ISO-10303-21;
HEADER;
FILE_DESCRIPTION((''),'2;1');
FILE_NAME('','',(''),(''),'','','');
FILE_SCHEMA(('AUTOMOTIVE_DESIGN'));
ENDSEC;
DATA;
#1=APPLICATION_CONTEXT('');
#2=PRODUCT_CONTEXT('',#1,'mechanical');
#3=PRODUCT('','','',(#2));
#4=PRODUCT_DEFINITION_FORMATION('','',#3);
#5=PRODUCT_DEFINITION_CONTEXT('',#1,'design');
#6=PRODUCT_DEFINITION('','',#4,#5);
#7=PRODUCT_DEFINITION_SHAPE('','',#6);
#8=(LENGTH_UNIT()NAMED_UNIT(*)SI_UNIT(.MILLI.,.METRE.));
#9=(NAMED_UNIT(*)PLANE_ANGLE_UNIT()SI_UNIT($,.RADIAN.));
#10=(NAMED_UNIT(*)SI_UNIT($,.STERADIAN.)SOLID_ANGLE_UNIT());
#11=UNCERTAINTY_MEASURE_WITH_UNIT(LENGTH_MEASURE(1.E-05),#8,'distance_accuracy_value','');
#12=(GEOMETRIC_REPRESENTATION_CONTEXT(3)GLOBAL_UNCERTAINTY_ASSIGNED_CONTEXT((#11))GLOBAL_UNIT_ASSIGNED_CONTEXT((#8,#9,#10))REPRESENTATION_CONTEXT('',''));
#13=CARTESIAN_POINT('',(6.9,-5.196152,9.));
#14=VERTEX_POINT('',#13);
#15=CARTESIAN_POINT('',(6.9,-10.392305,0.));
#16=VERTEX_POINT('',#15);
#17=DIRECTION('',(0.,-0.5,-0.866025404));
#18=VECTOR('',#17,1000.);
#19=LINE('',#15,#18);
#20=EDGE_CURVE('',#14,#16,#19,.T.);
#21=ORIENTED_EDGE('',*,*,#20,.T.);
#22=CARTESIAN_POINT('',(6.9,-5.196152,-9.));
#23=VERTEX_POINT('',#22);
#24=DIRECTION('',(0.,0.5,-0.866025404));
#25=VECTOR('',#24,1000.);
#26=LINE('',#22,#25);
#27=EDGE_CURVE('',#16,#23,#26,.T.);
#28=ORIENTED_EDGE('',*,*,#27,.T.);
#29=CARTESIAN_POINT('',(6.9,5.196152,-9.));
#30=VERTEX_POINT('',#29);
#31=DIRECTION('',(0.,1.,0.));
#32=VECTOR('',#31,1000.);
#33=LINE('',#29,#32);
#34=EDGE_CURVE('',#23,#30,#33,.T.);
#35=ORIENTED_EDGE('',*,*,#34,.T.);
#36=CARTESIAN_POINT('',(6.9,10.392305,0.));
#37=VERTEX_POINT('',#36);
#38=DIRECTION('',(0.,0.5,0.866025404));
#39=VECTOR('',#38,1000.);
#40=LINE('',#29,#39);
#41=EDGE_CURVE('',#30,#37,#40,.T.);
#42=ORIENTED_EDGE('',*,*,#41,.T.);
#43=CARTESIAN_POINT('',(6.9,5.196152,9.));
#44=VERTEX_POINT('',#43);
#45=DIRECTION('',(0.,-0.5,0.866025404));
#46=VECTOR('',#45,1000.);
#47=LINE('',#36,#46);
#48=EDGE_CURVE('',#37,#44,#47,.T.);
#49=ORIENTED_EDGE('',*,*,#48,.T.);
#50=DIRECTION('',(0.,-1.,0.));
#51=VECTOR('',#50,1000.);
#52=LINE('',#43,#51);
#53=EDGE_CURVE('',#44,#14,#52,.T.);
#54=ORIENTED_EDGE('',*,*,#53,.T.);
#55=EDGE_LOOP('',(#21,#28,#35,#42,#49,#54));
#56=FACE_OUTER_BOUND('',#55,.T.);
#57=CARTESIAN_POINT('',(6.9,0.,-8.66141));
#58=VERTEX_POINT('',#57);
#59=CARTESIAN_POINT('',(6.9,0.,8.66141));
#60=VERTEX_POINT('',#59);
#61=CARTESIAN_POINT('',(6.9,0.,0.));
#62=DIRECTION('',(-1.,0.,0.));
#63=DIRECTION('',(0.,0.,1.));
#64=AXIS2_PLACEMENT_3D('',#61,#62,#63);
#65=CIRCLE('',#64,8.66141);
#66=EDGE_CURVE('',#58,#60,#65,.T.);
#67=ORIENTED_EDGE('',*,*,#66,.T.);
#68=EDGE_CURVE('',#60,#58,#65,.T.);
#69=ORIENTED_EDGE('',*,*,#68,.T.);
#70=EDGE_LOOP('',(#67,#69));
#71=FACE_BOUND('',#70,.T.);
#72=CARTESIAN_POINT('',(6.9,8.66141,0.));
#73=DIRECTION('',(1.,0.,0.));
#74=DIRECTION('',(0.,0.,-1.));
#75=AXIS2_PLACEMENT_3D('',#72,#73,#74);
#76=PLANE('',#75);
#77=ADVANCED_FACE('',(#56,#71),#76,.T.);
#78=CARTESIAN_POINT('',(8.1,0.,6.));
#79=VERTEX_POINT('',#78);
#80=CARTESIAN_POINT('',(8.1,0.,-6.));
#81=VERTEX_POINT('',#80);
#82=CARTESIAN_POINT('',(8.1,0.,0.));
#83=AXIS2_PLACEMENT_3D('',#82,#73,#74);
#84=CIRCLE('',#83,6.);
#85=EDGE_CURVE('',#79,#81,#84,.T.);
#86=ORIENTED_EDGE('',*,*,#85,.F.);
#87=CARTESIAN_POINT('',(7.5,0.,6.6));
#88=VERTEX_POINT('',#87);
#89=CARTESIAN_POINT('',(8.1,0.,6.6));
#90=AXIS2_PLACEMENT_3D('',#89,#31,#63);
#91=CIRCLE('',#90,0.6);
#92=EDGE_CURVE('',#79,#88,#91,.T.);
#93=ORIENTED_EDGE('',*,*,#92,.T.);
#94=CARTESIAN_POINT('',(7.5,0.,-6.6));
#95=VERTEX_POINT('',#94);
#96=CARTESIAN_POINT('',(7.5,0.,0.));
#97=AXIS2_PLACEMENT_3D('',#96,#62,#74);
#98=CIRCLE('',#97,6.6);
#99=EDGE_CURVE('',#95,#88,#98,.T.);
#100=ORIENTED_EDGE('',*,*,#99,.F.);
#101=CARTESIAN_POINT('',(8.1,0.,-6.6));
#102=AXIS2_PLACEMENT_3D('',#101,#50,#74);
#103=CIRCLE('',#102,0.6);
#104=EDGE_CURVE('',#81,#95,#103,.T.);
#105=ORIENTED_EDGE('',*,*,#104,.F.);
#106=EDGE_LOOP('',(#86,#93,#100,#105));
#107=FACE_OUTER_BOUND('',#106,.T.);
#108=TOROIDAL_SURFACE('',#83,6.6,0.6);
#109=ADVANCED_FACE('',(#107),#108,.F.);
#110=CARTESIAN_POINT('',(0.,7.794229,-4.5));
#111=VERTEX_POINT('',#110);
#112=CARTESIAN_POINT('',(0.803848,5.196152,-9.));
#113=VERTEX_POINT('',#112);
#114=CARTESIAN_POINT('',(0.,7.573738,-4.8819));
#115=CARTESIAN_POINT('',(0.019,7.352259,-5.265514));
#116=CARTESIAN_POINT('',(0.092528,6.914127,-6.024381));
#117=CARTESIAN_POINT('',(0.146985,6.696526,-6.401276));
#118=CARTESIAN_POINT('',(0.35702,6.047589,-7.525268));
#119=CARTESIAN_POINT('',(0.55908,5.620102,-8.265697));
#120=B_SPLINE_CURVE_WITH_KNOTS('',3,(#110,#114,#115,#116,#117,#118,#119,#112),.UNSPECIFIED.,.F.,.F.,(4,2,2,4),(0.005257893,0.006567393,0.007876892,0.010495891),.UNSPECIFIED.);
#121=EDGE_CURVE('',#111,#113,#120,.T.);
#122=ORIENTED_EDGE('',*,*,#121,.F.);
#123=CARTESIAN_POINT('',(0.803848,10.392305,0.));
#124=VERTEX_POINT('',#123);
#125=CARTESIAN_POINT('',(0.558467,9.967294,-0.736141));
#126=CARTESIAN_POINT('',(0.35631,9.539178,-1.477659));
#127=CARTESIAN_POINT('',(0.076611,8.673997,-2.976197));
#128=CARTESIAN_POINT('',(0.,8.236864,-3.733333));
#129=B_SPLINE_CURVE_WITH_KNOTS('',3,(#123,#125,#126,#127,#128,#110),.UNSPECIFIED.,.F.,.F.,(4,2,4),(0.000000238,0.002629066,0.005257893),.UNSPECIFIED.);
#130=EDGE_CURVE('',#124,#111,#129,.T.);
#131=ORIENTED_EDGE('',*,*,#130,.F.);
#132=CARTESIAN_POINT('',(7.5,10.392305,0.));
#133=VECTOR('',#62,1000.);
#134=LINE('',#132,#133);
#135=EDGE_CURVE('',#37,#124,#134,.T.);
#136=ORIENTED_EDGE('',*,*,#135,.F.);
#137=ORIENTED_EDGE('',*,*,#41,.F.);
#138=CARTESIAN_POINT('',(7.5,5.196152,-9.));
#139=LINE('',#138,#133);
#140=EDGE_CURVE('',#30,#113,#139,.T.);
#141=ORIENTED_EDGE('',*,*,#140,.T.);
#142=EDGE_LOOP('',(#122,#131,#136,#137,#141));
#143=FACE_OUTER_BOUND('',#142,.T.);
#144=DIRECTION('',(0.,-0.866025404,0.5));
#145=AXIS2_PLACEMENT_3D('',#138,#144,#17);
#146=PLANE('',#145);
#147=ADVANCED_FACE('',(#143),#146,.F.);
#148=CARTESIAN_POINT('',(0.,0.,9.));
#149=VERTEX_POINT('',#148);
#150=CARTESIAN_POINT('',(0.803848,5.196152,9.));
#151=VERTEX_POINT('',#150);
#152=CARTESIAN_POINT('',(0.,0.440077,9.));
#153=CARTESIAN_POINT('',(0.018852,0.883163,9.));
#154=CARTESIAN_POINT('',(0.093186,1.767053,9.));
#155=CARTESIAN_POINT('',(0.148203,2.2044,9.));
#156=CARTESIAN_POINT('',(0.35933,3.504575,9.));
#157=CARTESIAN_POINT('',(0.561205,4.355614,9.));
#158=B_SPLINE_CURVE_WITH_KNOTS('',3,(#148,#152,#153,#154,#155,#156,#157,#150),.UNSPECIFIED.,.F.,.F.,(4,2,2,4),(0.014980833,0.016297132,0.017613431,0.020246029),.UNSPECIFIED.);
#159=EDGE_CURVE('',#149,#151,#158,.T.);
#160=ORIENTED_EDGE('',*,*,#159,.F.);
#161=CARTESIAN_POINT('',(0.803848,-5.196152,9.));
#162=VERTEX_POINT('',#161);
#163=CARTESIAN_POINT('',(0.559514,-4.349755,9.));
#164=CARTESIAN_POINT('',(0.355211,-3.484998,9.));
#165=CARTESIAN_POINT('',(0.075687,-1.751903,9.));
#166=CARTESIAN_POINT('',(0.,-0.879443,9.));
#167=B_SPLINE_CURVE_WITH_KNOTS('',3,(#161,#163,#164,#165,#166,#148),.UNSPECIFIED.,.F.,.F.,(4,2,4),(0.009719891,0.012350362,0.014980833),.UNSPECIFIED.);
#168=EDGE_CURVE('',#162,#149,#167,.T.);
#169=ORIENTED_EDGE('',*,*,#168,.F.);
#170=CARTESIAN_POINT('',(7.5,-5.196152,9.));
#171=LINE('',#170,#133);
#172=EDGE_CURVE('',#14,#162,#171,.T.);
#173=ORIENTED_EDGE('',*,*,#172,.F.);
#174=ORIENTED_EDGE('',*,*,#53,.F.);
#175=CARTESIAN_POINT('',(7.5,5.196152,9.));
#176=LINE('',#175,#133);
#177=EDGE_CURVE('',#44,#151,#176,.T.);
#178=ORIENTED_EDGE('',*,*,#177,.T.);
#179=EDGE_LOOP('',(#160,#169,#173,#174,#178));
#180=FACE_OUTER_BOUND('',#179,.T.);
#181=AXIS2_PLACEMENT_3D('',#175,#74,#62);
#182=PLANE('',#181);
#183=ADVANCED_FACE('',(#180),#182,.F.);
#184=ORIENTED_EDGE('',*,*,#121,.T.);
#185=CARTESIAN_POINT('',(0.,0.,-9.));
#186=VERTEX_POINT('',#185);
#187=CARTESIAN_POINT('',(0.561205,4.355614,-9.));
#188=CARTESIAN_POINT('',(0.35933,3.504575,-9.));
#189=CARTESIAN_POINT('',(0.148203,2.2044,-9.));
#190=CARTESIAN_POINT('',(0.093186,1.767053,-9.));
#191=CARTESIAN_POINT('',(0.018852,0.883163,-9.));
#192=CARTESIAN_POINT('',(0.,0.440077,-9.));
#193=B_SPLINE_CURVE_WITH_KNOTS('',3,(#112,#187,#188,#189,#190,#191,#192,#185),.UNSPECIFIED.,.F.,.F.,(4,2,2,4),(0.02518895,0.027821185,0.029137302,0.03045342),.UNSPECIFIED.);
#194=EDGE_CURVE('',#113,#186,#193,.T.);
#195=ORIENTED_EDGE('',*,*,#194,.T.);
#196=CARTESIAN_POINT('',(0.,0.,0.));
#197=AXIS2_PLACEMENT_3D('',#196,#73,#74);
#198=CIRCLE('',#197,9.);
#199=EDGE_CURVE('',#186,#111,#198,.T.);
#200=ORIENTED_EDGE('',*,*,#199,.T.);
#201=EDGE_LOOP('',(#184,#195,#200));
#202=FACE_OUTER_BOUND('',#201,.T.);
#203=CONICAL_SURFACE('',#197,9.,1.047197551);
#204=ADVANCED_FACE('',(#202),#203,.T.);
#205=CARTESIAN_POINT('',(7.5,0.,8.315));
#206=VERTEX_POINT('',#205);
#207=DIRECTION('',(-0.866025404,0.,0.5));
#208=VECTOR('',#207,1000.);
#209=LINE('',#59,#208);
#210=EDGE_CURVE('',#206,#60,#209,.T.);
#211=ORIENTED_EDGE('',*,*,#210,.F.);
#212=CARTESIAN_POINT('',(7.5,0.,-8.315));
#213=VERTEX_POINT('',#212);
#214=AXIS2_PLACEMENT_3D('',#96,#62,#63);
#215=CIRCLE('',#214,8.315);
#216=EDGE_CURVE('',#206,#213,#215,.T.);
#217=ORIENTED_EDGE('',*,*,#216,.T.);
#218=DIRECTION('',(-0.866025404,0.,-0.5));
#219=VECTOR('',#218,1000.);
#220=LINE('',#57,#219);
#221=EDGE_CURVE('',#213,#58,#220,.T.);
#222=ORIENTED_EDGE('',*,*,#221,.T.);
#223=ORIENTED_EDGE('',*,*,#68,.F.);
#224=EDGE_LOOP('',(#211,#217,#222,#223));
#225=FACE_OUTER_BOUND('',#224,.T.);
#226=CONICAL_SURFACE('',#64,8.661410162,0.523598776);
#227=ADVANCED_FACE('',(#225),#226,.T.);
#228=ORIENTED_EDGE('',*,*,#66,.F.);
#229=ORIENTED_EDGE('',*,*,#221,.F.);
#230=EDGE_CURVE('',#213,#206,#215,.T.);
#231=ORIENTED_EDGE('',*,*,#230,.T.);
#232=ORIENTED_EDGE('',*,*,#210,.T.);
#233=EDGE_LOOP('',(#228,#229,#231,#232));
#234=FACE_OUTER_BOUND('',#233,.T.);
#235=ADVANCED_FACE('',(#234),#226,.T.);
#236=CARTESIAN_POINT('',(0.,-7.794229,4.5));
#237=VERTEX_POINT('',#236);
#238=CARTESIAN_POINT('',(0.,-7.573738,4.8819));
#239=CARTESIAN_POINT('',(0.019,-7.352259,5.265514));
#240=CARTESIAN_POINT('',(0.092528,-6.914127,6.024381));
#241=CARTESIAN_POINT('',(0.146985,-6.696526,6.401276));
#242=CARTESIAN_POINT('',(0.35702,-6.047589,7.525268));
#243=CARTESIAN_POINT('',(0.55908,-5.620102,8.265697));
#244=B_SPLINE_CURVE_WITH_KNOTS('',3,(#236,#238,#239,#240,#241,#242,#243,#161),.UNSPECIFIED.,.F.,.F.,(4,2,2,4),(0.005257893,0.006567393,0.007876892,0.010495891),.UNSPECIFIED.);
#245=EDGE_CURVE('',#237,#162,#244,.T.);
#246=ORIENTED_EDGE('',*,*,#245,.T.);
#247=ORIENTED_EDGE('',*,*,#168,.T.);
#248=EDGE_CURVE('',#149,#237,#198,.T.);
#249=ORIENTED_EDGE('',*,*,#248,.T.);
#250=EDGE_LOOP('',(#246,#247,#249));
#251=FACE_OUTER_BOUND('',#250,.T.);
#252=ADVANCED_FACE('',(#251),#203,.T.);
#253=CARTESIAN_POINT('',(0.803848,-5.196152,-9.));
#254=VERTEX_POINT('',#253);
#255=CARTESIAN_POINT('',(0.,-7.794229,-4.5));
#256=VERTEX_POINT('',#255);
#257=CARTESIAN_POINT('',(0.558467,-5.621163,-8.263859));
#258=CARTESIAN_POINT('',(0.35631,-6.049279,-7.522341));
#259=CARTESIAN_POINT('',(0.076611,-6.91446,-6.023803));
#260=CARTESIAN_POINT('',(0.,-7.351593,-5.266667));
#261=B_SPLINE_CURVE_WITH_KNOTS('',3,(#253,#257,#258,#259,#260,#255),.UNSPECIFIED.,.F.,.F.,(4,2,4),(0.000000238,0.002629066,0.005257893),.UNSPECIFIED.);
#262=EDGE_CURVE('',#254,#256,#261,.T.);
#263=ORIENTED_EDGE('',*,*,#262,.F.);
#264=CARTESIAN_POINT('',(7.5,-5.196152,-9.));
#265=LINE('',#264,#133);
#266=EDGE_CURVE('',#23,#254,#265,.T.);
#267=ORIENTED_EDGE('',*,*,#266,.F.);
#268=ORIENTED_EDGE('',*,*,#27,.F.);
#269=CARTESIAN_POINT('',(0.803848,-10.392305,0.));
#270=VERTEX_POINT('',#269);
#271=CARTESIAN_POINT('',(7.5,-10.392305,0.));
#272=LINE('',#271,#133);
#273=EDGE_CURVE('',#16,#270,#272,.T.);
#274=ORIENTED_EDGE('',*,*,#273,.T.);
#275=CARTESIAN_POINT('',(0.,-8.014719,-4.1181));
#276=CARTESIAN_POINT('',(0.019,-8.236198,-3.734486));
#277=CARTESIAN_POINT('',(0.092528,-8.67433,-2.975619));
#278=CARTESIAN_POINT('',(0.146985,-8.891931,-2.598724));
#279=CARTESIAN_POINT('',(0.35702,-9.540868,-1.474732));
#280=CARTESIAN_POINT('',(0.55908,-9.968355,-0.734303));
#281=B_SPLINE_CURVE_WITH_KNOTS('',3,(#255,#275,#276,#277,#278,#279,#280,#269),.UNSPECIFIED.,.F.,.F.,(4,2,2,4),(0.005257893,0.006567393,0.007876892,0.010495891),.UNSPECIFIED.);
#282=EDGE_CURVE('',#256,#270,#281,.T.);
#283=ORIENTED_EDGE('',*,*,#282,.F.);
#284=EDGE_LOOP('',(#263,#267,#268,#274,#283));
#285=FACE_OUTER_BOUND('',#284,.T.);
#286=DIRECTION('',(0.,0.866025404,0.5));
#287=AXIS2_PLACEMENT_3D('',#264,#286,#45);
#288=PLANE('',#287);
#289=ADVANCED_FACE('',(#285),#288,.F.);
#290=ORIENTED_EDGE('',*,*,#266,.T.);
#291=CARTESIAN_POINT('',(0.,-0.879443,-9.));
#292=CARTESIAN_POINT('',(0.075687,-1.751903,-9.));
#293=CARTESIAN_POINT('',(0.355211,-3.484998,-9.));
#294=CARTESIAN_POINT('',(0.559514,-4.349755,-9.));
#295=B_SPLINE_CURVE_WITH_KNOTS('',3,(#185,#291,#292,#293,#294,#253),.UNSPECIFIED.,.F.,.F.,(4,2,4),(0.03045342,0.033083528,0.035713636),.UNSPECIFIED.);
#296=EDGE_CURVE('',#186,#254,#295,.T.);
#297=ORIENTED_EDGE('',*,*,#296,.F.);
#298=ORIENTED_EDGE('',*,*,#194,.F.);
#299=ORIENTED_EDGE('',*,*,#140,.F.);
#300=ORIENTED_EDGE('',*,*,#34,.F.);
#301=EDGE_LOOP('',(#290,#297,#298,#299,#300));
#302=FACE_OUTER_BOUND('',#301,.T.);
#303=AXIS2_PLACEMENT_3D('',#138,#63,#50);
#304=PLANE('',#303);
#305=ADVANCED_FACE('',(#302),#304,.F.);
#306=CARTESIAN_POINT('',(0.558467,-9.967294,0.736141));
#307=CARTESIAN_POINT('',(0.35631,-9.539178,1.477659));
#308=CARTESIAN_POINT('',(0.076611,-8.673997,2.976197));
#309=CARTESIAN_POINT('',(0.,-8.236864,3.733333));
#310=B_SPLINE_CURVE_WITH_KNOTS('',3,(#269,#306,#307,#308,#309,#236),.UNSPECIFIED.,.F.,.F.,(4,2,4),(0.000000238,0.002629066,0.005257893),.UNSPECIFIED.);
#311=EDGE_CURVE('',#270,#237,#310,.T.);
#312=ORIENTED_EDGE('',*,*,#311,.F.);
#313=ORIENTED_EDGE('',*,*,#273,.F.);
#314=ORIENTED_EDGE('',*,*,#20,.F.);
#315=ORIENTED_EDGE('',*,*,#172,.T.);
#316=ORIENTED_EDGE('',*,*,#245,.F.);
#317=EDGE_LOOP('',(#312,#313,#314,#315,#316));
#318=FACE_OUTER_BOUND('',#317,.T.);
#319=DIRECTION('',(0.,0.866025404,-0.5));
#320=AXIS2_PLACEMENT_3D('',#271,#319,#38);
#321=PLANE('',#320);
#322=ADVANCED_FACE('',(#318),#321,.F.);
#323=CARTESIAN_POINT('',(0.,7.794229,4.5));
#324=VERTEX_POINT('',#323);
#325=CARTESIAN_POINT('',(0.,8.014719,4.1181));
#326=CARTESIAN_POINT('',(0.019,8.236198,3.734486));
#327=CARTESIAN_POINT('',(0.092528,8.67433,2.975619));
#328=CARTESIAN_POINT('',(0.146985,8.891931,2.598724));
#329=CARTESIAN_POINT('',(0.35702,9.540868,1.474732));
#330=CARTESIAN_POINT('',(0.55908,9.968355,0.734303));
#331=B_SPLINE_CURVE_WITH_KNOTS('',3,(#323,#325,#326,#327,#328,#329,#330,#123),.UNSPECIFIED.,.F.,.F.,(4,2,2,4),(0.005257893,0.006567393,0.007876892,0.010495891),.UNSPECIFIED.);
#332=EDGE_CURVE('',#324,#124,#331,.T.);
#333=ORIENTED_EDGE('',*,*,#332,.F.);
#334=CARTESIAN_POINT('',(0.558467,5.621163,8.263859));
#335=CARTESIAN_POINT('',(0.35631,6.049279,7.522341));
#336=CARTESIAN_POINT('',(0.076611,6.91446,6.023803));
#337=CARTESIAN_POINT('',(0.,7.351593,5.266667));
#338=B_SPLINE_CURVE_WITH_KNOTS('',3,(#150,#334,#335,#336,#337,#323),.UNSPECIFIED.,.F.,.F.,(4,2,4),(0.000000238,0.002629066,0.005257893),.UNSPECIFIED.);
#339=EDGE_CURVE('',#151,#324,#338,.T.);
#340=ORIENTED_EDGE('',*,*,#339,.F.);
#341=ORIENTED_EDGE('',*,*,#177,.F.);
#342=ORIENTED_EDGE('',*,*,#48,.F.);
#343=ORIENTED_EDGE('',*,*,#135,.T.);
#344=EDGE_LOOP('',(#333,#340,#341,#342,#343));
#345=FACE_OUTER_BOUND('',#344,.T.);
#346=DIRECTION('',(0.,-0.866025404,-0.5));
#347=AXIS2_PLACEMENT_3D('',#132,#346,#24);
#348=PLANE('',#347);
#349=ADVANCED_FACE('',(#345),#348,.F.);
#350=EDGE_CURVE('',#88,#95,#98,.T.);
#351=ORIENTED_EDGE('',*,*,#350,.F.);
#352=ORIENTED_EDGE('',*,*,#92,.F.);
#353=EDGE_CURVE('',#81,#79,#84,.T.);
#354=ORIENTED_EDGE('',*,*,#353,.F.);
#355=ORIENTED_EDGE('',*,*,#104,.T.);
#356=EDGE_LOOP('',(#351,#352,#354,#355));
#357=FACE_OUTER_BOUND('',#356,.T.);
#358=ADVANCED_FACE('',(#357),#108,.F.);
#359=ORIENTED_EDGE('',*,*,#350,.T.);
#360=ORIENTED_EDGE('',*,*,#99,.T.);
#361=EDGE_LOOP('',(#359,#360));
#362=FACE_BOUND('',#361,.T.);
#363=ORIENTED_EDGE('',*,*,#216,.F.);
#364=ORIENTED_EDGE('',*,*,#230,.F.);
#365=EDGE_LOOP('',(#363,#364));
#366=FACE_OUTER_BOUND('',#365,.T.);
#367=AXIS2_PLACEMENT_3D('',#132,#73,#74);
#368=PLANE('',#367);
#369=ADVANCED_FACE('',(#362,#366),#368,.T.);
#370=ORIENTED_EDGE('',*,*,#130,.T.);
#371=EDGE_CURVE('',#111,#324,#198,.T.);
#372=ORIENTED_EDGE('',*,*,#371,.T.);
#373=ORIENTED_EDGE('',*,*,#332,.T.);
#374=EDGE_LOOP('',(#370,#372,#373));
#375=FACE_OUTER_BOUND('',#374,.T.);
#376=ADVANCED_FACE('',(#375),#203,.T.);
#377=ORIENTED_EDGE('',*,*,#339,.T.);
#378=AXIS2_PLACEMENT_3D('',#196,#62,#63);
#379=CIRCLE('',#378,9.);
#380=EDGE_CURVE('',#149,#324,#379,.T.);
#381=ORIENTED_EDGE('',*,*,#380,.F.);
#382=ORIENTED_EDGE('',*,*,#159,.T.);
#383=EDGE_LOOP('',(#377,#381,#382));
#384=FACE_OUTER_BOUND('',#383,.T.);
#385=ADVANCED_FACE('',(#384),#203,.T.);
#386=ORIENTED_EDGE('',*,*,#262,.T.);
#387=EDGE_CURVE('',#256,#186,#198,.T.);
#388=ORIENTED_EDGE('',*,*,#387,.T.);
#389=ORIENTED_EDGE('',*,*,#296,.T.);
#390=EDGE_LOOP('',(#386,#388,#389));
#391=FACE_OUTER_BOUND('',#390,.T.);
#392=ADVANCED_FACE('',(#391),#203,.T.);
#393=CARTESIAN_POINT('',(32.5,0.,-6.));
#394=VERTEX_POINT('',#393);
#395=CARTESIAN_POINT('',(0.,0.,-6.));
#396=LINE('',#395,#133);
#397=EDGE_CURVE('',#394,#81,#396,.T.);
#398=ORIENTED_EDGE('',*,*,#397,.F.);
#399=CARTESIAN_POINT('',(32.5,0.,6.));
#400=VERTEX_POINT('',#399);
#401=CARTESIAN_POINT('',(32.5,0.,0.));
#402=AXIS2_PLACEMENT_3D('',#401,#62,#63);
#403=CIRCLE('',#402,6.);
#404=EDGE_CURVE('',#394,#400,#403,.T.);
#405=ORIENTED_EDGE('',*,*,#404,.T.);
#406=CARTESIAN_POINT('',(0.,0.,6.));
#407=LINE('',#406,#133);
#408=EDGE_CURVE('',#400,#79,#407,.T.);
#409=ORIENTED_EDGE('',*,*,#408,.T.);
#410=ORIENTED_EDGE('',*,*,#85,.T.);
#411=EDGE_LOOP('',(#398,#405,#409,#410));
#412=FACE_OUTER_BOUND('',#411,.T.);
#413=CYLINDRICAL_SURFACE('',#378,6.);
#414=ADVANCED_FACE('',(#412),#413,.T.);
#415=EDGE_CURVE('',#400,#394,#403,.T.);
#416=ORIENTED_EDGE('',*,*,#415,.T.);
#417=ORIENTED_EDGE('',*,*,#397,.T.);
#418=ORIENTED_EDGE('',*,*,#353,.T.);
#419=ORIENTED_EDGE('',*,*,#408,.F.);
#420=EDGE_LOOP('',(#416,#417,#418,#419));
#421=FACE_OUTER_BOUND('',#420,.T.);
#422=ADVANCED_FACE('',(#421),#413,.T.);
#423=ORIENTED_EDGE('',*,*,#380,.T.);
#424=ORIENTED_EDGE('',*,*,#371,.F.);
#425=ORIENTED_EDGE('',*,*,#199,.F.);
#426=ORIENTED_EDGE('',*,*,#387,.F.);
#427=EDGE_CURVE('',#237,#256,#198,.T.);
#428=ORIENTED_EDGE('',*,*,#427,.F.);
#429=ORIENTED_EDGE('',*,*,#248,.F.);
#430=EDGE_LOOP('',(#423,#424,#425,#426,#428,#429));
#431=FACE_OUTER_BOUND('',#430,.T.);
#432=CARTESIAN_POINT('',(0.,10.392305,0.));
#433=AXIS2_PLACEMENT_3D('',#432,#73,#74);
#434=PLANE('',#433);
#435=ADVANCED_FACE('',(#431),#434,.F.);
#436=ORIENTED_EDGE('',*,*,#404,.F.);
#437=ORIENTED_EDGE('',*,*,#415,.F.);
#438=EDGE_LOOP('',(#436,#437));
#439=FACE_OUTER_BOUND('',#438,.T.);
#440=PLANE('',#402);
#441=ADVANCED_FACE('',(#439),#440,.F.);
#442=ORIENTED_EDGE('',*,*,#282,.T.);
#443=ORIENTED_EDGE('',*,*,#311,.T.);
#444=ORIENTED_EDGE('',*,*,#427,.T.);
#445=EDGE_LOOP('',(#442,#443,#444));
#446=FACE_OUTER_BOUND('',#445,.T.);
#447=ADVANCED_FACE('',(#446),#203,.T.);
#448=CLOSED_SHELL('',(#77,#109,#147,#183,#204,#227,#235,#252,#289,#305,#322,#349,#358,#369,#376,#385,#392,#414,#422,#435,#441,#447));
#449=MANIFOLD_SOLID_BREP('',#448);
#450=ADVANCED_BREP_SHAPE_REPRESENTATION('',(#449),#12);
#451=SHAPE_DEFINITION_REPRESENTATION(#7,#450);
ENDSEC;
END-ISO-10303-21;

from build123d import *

# Parameters (mm, degrees)
EXTRUDE_387_DEPTH = 7.5
FILLET_1280_R     = 0.6


with BuildPart() as part:
    # 草图1 → Extrude 387 (new body)
    with BuildSketch(Plane(origin=(0, 0, 0), x_dir=(0, 0, -1), z_dir=(1, 0, 0))):
        Polygon((9, 5.196152423), (9, -5.196152423), (0, -10.392304845), (-9, -5.196152423), (-9, 5.196152423), (0, 10.392304845), align=None)
    extrude(amount=EXTRUDE_387_DEPTH)

    # 草图2 → 凸台-旋转1 (revolve)
    with BuildSketch(Plane.XY, mode=Mode.PRIVATE) as revolve_1_sk:
        Polygon((0, 0), (32.5, 0), (32.5, 4.4845), (32.5, 6), (2.5, 6), (0, 6), align=None)
    revolve(revolve_1_sk.sketch.rotate(Axis((0, 0, 0), (1, 0, 0)), 90), axis=Axis((0, 0, 0), (1, 0, 0)))

    # 草图3 → 切除-旋转1 (revolve, cut)
    with BuildSketch(Plane.XY):
        Polygon((0, 9), (3.690598923, 15.392304845), (3.690598923, 20.392304845), (-10, 20.392304845), (-10, 9), align=None)
    revolve(axis=Axis((0, 0, 0), (1, 0, 0)), mode=Mode.SUBTRACT)

    # 草图4 → 切除-旋转3 (revolve, cut)
    with BuildSketch(Plane.XY, mode=Mode.PRIVATE) as cut_revolve_3_sk:
        Polygon((7.5, 8.315), (6.9, 8.661410162), (6.9, 10.392304845), (7.5, 10.392304845), align=None)
    revolve(cut_revolve_3_sk.sketch.rotate(Axis((0, 0, 0), (1, 0, 0)), 90), axis=Axis((0, 0, 0), (1, 0, 0)), mode=Mode.SUBTRACT)

    # Fillet 1280
    fillet_1280_edges = [part.edges().sort_by_distance(p)[0] for p in [
        (7.5, 0, -6),
    ]]
    fillet(fillet_1280_edges, radius=FILLET_1280_R)


solid = part.part
